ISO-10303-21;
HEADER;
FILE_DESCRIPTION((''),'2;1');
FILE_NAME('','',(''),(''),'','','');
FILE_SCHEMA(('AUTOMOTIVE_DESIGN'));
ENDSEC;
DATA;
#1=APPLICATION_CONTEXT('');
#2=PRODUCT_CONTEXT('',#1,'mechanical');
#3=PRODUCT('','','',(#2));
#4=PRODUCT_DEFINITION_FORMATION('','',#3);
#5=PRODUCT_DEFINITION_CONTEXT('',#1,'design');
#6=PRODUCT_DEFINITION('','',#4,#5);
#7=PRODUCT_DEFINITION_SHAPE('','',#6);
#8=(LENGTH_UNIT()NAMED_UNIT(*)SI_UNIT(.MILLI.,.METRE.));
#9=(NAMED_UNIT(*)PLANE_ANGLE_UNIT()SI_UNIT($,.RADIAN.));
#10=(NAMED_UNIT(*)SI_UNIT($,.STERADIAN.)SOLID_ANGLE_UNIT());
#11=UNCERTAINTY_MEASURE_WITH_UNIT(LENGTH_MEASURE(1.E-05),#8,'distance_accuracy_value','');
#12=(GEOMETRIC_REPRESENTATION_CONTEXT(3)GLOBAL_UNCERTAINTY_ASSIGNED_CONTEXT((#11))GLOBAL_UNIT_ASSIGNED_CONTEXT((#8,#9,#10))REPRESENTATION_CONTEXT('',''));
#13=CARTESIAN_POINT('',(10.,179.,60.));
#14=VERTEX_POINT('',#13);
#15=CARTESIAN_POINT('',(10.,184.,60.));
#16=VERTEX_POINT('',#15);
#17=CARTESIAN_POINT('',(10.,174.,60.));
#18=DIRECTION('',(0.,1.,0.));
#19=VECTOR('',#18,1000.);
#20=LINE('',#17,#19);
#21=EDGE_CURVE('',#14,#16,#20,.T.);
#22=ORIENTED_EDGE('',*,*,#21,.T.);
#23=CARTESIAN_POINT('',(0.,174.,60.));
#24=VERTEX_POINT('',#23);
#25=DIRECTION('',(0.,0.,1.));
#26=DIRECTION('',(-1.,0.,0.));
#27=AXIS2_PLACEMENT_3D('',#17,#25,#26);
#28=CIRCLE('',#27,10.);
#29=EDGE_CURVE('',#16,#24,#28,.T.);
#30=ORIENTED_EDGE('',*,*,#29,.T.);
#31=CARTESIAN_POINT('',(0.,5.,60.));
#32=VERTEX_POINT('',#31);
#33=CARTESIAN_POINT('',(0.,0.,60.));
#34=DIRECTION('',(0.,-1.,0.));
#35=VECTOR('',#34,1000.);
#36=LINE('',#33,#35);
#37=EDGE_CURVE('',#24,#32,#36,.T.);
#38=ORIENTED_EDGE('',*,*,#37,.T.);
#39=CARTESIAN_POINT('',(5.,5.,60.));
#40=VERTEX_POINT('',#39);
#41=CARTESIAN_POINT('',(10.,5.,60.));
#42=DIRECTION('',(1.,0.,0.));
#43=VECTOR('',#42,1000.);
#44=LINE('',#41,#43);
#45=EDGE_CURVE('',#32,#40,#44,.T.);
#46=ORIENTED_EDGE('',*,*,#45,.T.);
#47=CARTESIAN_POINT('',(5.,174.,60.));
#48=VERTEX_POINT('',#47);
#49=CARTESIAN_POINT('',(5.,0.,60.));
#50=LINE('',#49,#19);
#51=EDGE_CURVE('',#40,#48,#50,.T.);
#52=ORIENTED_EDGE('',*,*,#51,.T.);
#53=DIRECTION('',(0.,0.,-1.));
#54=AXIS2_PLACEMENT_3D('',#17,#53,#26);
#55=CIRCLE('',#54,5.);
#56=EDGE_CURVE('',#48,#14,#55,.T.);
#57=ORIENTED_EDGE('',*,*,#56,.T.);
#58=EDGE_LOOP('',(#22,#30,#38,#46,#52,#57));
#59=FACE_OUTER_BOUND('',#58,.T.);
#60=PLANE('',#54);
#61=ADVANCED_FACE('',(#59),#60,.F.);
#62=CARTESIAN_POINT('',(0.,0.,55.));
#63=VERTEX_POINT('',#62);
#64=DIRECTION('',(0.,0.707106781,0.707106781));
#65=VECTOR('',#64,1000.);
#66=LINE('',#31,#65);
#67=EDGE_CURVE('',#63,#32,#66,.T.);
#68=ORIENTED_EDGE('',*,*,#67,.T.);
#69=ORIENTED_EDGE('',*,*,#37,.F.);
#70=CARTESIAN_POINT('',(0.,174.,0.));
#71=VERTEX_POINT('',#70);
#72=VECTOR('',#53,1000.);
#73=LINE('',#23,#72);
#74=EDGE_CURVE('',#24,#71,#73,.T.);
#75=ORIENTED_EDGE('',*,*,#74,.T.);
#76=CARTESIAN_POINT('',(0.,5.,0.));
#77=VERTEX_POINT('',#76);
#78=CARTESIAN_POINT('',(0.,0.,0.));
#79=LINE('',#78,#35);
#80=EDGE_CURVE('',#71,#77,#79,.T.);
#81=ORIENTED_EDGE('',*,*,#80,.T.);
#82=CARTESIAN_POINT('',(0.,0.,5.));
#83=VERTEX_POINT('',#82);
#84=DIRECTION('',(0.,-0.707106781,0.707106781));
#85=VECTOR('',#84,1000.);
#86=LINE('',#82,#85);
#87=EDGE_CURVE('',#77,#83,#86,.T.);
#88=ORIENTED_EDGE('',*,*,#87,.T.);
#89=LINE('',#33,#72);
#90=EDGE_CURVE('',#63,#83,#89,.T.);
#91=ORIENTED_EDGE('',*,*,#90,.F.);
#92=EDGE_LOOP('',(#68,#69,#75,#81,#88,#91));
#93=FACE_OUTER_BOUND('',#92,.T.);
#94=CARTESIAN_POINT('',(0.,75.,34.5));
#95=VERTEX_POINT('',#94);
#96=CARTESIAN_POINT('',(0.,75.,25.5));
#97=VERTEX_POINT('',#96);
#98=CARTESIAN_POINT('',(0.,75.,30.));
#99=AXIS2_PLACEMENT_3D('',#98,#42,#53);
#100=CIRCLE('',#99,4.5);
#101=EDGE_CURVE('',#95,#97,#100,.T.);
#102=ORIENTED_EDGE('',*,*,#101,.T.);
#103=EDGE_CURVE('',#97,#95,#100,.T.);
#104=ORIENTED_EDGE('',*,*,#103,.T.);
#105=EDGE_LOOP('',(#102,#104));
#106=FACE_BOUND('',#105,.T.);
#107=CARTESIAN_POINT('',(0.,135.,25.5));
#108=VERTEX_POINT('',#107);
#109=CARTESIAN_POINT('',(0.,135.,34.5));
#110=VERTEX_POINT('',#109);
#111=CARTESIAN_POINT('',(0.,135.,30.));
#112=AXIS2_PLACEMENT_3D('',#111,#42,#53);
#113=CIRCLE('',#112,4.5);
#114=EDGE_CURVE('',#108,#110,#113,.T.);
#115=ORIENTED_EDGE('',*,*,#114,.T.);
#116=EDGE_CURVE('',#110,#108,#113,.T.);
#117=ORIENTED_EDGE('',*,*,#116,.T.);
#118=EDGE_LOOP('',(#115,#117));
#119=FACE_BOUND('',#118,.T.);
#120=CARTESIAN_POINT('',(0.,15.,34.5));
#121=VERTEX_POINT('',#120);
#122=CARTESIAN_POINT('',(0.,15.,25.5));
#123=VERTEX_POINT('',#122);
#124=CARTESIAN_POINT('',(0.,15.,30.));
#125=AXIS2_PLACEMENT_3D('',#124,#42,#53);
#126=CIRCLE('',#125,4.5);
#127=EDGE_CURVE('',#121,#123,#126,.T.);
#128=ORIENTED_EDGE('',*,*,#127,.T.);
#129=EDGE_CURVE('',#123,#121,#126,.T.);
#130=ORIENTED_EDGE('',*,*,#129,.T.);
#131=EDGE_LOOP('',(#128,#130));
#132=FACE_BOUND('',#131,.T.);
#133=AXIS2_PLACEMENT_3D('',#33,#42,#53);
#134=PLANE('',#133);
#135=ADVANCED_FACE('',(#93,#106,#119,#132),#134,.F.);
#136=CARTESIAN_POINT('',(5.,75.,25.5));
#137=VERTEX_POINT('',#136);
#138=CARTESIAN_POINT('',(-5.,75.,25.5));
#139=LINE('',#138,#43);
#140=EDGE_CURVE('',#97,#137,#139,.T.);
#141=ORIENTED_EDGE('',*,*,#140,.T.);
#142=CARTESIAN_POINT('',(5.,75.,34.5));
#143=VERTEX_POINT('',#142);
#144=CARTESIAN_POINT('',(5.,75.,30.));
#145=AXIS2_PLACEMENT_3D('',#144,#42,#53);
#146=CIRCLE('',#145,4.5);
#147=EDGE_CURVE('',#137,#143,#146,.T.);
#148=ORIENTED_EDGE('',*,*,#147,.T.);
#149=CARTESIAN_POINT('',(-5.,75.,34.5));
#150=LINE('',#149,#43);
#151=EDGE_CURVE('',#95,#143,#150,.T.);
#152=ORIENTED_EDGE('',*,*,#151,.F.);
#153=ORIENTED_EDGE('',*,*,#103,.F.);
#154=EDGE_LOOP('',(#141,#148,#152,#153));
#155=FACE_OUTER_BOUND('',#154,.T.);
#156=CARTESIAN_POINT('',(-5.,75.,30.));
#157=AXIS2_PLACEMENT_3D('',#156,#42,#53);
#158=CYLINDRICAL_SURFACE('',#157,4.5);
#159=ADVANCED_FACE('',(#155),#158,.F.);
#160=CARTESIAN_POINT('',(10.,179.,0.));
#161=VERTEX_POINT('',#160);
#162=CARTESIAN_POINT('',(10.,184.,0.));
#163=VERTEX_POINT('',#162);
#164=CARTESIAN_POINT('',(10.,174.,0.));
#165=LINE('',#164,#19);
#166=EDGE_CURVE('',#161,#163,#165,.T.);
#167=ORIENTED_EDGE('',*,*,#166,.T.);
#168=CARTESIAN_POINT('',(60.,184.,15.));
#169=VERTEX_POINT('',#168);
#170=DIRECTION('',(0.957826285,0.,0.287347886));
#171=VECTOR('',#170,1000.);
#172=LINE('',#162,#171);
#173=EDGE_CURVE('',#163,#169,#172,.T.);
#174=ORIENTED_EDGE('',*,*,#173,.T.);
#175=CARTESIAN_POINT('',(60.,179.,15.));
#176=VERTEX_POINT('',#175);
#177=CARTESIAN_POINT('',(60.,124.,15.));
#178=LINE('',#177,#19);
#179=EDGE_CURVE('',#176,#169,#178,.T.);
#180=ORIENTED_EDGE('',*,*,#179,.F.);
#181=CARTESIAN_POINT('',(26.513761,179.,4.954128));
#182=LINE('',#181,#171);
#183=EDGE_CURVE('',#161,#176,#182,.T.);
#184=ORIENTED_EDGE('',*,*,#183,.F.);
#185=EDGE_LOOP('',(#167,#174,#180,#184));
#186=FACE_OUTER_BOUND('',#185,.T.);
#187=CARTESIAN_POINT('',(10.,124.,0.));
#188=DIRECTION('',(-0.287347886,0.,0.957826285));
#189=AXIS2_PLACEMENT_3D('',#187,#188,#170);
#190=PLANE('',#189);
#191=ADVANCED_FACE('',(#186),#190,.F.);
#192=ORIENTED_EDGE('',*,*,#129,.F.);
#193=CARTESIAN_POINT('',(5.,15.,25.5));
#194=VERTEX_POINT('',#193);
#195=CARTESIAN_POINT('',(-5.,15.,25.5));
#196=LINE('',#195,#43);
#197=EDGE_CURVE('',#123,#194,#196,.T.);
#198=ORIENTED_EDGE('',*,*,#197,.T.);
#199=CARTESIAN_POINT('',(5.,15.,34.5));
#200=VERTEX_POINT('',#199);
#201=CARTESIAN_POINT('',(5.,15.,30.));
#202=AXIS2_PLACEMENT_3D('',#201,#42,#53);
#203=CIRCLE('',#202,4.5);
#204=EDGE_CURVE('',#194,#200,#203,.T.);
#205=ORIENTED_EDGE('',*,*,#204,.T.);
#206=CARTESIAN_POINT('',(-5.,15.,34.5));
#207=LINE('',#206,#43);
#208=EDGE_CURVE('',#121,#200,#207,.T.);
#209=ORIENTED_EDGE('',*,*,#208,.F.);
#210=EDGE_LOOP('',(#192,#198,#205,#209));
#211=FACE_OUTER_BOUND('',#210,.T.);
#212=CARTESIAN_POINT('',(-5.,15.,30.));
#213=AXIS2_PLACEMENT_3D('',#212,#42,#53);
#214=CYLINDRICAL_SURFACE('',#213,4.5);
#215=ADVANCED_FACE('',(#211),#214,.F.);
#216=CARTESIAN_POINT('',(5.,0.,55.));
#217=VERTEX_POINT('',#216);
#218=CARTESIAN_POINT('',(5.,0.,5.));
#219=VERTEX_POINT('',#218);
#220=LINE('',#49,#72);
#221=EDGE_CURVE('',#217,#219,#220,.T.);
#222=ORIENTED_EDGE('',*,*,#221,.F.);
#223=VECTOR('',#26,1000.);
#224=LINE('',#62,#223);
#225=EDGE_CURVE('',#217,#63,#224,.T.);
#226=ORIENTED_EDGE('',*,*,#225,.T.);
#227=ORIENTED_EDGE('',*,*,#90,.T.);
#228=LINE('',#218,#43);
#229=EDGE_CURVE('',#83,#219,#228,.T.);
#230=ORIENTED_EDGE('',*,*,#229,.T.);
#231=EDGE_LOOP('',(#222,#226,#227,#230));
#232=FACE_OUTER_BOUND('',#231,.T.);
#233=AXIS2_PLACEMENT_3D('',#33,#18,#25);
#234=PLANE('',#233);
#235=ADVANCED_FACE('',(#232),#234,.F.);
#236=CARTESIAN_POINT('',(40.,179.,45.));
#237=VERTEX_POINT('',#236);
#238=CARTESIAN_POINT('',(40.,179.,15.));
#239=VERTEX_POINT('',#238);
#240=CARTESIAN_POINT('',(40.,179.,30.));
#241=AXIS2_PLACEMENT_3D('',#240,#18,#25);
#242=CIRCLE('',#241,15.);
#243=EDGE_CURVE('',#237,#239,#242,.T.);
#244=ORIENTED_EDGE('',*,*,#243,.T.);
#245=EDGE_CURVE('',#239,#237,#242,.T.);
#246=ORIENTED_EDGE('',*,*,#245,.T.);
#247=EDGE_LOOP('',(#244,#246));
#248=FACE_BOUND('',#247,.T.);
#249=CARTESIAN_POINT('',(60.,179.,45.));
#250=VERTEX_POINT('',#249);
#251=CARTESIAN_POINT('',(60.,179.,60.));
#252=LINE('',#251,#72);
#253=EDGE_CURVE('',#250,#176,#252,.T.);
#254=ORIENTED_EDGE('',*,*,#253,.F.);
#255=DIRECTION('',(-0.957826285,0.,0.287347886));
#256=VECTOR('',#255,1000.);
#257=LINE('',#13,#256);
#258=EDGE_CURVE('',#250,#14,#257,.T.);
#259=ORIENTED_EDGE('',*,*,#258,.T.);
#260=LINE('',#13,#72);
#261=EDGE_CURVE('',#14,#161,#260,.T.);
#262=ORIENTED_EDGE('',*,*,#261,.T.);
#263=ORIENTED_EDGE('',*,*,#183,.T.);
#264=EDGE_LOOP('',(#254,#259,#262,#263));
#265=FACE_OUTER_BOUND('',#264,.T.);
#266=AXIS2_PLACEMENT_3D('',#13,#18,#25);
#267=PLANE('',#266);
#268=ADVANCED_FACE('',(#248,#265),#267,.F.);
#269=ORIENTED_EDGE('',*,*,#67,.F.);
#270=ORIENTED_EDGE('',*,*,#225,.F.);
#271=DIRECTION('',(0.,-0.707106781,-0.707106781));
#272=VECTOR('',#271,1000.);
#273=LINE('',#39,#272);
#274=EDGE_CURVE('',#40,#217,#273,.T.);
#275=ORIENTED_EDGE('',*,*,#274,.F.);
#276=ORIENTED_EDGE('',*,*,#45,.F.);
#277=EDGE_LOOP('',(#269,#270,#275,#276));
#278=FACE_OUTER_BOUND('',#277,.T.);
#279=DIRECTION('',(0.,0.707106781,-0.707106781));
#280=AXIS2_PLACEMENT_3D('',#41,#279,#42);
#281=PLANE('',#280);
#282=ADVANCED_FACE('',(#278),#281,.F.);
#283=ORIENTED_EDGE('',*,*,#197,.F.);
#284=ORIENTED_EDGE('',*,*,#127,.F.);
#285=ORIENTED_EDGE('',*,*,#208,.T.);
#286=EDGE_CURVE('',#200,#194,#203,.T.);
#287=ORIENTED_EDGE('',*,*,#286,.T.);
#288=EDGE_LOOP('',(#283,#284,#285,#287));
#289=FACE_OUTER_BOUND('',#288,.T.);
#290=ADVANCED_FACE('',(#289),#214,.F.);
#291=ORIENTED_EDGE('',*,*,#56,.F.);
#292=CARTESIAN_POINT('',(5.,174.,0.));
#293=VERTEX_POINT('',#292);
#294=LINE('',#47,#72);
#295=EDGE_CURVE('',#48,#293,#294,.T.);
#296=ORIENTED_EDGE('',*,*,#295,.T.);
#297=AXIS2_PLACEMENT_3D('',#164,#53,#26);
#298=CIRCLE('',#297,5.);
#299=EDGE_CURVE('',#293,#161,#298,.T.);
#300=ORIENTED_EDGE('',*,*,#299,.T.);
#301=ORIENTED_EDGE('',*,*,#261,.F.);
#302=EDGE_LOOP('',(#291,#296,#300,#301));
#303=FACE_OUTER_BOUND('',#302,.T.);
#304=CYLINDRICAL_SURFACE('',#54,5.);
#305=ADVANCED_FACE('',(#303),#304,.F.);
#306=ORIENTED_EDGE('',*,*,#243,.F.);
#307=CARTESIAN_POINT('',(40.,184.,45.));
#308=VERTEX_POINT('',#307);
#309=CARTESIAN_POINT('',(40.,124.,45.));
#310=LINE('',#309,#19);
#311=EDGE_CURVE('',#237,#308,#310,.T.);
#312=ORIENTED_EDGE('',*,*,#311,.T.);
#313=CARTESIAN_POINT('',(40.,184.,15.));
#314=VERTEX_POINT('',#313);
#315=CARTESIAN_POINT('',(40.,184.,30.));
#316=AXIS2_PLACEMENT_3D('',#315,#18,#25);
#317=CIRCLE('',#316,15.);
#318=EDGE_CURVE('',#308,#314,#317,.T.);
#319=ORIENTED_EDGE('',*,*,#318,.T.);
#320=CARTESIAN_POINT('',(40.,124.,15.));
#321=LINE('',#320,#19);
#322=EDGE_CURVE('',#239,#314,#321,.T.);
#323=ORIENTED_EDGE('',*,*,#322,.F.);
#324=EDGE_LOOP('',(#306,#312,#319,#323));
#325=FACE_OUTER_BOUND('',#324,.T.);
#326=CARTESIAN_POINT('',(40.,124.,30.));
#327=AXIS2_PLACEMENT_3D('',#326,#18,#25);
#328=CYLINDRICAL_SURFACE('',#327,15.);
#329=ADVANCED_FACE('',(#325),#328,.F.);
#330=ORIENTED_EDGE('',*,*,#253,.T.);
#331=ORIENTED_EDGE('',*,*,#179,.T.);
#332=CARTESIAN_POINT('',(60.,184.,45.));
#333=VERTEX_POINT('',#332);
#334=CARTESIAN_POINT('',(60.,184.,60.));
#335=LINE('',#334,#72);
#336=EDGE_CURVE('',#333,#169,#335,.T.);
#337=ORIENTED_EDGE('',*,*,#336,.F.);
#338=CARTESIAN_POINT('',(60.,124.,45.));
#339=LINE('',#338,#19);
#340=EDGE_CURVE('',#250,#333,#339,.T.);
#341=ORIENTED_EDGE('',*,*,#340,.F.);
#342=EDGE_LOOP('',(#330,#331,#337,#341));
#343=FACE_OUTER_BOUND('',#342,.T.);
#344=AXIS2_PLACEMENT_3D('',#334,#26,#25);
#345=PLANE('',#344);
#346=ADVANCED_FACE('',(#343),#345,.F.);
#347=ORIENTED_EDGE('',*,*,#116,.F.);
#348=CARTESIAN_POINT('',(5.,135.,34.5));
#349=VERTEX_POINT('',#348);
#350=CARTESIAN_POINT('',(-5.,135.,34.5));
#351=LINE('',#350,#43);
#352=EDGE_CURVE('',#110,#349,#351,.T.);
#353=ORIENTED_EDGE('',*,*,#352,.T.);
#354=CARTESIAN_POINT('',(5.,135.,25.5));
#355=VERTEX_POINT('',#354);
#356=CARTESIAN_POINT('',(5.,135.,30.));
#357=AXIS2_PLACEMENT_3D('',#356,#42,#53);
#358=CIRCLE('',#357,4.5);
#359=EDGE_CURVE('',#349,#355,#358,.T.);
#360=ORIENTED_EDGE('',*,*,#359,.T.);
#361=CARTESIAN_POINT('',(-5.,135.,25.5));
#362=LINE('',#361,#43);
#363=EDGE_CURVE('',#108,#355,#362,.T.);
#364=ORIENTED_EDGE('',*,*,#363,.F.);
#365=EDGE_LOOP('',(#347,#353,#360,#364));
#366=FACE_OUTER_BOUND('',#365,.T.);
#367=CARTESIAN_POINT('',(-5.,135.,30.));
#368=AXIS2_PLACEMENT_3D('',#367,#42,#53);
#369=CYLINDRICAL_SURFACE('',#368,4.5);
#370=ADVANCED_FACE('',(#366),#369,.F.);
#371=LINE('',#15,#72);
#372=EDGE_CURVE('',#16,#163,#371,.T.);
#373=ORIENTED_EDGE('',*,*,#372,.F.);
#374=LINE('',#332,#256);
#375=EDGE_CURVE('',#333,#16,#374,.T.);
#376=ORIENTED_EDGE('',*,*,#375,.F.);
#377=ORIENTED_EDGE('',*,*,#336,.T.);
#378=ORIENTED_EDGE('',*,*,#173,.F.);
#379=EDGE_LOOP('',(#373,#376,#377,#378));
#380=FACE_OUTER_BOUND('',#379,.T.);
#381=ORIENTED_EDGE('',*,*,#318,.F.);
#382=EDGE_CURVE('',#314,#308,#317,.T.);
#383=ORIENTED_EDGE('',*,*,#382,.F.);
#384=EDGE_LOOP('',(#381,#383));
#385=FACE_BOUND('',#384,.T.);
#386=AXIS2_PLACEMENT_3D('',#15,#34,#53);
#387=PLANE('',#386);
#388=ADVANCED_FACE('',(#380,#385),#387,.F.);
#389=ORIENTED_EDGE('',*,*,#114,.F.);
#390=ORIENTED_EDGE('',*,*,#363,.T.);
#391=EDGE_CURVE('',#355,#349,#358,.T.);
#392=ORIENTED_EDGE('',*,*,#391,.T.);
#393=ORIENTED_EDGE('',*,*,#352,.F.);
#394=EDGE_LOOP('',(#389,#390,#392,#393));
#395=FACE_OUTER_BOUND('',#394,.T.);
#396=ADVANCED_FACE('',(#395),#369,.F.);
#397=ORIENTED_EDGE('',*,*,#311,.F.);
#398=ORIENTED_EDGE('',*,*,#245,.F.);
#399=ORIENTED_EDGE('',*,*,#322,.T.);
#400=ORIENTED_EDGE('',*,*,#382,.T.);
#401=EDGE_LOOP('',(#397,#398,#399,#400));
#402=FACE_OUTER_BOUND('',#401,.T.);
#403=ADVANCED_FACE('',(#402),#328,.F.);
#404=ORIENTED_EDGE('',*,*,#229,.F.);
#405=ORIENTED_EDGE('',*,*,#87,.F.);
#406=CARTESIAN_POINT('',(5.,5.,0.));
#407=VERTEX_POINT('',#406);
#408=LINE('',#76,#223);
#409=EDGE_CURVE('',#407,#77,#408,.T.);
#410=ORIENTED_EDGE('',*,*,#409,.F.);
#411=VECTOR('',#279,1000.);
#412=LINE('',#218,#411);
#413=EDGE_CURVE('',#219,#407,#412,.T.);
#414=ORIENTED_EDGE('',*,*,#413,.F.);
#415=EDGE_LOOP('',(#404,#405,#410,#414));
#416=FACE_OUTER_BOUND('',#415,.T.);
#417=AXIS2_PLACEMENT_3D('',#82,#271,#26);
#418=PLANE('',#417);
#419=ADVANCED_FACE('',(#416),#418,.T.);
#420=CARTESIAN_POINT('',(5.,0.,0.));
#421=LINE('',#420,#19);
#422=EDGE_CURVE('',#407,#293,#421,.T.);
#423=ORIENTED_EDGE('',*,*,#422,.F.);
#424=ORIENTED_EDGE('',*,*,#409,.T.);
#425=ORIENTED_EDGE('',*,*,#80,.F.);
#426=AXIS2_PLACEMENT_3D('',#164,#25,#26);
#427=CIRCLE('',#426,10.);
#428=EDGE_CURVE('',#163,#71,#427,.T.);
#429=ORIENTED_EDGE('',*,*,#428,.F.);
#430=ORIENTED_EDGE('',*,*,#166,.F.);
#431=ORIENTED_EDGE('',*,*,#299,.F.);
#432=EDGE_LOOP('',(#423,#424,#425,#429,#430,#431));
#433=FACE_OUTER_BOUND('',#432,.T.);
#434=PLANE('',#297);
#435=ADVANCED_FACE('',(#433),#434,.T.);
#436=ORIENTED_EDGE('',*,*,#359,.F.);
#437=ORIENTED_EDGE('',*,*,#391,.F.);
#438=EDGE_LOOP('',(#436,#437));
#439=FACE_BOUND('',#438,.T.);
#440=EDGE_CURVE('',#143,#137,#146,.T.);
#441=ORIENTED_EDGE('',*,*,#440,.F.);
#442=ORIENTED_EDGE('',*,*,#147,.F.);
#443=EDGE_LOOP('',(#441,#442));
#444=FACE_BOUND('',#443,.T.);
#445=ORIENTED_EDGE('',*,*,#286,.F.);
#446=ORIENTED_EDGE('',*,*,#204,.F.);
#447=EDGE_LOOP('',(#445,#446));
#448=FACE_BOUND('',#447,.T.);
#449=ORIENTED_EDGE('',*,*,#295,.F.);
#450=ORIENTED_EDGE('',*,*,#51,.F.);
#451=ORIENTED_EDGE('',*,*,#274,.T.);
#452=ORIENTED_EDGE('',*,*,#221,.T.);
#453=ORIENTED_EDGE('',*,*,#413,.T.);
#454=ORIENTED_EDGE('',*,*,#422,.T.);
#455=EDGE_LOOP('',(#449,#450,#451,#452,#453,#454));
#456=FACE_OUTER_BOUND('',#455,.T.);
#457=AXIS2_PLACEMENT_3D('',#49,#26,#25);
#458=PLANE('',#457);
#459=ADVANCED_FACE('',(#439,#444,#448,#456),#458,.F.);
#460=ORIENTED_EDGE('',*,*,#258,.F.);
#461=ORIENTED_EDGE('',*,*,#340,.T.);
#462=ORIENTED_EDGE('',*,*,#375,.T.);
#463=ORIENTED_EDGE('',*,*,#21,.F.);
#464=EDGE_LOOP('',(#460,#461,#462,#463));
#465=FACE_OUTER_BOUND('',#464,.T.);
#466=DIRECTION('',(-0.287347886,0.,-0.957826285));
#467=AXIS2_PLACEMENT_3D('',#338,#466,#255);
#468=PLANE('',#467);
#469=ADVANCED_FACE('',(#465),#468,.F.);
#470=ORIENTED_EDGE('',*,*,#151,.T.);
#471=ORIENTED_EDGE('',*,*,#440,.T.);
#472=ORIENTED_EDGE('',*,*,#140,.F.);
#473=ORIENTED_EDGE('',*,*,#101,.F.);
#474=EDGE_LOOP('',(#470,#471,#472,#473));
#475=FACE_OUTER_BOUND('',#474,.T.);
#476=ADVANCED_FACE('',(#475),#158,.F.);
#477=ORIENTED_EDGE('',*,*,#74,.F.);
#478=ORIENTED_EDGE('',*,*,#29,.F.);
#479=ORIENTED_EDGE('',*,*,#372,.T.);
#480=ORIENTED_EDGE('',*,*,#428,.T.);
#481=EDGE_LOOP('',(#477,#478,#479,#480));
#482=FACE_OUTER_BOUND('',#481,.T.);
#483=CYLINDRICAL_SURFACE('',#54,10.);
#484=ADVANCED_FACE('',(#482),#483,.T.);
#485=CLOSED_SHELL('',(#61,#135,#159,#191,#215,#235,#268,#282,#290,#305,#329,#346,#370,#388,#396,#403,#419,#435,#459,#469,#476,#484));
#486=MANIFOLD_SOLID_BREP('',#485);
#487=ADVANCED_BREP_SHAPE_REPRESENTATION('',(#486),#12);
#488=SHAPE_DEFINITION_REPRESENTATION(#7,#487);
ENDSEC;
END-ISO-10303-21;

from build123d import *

# Parameters (mm, degrees)
BOSS_EXTRUDE1_DEPTH = 60
CHAMFER1_SIZE       = 5
SKETCH5_R           = 15
CUT_EXTRUDE1_DEPTH  = 60
CUT_EXTRUDE2_DEPTH  = 60
SKETCH3_R           = 4.5
CUT_EXTRUDE3_DEPTH  = 10


with BuildPart() as part:
    # Sketch1 → Boss-Extrude1 (new body)
    with BuildSketch(Plane.XY):
        with BuildLine():
            Line((0, 0), (0, 174))
            ThreePointArc((0, 174), (2.928932188, 181.071067812), (10, 184))
            Line((10, 184), (60, 184))
            Line((60, 184), (60, 179))
            Line((60, 179), (10, 179))
            ThreePointArc((10, 179), (6.464466094, 177.535533906), (5, 174))
            Line((5, 174), (5, 0))
            Line((5, 0), (0, 0))
        make_face()
    extrude(amount=BOSS_EXTRUDE1_DEPTH)

    # Chamfer1
    chamfer1_edges = [part.edges().sort_by_distance(p)[0] for p in [
        (2.5, 0, 0),
        (2.5, 0, 60),
    ]]
    chamfer(chamfer1_edges, length=CHAMFER1_SIZE)

    # Sketch5 → Cut-Extrude1 (cut)
    with BuildSketch(Plane(origin=(0, 184, 0), x_dir=(1, 0, 0), z_dir=(0, 1, 0))):
        with Locations(Location((40, -30, 0), (0, 0, 270))):
            Circle(SKETCH5_R)
    extrude(amount=-CUT_EXTRUDE1_DEPTH, mode=Mode.SUBTRACT)

    # Sketch6 → Cut-Extrude2 (cut)
    with BuildSketch(Plane(origin=(0, 184, 0), x_dir=(1, 0, 0), z_dir=(0, 1, 0))):
        Polygon((10, 0), (60, -15), (60, 0), align=None)
        Polygon((60, -45), (10, -60), (60, -60), align=None)
    extrude(amount=-CUT_EXTRUDE2_DEPTH, mode=Mode.SUBTRACT)

    # Sketch3 → Cut-Extrude3 (cut)
    with BuildSketch(Plane(origin=(5, 0, 0), x_dir=(0, 0, -1), z_dir=(1, 0, 0))):
        with Locations((-30, 15)):
            Circle(SKETCH3_R)
        with Locations((-30, 75)):
            Circle(SKETCH3_R)
        with Locations((-30, 135)):
            Circle(SKETCH3_R)
    extrude(amount=-CUT_EXTRUDE3_DEPTH, mode=Mode.SUBTRACT)


solid = part.part
